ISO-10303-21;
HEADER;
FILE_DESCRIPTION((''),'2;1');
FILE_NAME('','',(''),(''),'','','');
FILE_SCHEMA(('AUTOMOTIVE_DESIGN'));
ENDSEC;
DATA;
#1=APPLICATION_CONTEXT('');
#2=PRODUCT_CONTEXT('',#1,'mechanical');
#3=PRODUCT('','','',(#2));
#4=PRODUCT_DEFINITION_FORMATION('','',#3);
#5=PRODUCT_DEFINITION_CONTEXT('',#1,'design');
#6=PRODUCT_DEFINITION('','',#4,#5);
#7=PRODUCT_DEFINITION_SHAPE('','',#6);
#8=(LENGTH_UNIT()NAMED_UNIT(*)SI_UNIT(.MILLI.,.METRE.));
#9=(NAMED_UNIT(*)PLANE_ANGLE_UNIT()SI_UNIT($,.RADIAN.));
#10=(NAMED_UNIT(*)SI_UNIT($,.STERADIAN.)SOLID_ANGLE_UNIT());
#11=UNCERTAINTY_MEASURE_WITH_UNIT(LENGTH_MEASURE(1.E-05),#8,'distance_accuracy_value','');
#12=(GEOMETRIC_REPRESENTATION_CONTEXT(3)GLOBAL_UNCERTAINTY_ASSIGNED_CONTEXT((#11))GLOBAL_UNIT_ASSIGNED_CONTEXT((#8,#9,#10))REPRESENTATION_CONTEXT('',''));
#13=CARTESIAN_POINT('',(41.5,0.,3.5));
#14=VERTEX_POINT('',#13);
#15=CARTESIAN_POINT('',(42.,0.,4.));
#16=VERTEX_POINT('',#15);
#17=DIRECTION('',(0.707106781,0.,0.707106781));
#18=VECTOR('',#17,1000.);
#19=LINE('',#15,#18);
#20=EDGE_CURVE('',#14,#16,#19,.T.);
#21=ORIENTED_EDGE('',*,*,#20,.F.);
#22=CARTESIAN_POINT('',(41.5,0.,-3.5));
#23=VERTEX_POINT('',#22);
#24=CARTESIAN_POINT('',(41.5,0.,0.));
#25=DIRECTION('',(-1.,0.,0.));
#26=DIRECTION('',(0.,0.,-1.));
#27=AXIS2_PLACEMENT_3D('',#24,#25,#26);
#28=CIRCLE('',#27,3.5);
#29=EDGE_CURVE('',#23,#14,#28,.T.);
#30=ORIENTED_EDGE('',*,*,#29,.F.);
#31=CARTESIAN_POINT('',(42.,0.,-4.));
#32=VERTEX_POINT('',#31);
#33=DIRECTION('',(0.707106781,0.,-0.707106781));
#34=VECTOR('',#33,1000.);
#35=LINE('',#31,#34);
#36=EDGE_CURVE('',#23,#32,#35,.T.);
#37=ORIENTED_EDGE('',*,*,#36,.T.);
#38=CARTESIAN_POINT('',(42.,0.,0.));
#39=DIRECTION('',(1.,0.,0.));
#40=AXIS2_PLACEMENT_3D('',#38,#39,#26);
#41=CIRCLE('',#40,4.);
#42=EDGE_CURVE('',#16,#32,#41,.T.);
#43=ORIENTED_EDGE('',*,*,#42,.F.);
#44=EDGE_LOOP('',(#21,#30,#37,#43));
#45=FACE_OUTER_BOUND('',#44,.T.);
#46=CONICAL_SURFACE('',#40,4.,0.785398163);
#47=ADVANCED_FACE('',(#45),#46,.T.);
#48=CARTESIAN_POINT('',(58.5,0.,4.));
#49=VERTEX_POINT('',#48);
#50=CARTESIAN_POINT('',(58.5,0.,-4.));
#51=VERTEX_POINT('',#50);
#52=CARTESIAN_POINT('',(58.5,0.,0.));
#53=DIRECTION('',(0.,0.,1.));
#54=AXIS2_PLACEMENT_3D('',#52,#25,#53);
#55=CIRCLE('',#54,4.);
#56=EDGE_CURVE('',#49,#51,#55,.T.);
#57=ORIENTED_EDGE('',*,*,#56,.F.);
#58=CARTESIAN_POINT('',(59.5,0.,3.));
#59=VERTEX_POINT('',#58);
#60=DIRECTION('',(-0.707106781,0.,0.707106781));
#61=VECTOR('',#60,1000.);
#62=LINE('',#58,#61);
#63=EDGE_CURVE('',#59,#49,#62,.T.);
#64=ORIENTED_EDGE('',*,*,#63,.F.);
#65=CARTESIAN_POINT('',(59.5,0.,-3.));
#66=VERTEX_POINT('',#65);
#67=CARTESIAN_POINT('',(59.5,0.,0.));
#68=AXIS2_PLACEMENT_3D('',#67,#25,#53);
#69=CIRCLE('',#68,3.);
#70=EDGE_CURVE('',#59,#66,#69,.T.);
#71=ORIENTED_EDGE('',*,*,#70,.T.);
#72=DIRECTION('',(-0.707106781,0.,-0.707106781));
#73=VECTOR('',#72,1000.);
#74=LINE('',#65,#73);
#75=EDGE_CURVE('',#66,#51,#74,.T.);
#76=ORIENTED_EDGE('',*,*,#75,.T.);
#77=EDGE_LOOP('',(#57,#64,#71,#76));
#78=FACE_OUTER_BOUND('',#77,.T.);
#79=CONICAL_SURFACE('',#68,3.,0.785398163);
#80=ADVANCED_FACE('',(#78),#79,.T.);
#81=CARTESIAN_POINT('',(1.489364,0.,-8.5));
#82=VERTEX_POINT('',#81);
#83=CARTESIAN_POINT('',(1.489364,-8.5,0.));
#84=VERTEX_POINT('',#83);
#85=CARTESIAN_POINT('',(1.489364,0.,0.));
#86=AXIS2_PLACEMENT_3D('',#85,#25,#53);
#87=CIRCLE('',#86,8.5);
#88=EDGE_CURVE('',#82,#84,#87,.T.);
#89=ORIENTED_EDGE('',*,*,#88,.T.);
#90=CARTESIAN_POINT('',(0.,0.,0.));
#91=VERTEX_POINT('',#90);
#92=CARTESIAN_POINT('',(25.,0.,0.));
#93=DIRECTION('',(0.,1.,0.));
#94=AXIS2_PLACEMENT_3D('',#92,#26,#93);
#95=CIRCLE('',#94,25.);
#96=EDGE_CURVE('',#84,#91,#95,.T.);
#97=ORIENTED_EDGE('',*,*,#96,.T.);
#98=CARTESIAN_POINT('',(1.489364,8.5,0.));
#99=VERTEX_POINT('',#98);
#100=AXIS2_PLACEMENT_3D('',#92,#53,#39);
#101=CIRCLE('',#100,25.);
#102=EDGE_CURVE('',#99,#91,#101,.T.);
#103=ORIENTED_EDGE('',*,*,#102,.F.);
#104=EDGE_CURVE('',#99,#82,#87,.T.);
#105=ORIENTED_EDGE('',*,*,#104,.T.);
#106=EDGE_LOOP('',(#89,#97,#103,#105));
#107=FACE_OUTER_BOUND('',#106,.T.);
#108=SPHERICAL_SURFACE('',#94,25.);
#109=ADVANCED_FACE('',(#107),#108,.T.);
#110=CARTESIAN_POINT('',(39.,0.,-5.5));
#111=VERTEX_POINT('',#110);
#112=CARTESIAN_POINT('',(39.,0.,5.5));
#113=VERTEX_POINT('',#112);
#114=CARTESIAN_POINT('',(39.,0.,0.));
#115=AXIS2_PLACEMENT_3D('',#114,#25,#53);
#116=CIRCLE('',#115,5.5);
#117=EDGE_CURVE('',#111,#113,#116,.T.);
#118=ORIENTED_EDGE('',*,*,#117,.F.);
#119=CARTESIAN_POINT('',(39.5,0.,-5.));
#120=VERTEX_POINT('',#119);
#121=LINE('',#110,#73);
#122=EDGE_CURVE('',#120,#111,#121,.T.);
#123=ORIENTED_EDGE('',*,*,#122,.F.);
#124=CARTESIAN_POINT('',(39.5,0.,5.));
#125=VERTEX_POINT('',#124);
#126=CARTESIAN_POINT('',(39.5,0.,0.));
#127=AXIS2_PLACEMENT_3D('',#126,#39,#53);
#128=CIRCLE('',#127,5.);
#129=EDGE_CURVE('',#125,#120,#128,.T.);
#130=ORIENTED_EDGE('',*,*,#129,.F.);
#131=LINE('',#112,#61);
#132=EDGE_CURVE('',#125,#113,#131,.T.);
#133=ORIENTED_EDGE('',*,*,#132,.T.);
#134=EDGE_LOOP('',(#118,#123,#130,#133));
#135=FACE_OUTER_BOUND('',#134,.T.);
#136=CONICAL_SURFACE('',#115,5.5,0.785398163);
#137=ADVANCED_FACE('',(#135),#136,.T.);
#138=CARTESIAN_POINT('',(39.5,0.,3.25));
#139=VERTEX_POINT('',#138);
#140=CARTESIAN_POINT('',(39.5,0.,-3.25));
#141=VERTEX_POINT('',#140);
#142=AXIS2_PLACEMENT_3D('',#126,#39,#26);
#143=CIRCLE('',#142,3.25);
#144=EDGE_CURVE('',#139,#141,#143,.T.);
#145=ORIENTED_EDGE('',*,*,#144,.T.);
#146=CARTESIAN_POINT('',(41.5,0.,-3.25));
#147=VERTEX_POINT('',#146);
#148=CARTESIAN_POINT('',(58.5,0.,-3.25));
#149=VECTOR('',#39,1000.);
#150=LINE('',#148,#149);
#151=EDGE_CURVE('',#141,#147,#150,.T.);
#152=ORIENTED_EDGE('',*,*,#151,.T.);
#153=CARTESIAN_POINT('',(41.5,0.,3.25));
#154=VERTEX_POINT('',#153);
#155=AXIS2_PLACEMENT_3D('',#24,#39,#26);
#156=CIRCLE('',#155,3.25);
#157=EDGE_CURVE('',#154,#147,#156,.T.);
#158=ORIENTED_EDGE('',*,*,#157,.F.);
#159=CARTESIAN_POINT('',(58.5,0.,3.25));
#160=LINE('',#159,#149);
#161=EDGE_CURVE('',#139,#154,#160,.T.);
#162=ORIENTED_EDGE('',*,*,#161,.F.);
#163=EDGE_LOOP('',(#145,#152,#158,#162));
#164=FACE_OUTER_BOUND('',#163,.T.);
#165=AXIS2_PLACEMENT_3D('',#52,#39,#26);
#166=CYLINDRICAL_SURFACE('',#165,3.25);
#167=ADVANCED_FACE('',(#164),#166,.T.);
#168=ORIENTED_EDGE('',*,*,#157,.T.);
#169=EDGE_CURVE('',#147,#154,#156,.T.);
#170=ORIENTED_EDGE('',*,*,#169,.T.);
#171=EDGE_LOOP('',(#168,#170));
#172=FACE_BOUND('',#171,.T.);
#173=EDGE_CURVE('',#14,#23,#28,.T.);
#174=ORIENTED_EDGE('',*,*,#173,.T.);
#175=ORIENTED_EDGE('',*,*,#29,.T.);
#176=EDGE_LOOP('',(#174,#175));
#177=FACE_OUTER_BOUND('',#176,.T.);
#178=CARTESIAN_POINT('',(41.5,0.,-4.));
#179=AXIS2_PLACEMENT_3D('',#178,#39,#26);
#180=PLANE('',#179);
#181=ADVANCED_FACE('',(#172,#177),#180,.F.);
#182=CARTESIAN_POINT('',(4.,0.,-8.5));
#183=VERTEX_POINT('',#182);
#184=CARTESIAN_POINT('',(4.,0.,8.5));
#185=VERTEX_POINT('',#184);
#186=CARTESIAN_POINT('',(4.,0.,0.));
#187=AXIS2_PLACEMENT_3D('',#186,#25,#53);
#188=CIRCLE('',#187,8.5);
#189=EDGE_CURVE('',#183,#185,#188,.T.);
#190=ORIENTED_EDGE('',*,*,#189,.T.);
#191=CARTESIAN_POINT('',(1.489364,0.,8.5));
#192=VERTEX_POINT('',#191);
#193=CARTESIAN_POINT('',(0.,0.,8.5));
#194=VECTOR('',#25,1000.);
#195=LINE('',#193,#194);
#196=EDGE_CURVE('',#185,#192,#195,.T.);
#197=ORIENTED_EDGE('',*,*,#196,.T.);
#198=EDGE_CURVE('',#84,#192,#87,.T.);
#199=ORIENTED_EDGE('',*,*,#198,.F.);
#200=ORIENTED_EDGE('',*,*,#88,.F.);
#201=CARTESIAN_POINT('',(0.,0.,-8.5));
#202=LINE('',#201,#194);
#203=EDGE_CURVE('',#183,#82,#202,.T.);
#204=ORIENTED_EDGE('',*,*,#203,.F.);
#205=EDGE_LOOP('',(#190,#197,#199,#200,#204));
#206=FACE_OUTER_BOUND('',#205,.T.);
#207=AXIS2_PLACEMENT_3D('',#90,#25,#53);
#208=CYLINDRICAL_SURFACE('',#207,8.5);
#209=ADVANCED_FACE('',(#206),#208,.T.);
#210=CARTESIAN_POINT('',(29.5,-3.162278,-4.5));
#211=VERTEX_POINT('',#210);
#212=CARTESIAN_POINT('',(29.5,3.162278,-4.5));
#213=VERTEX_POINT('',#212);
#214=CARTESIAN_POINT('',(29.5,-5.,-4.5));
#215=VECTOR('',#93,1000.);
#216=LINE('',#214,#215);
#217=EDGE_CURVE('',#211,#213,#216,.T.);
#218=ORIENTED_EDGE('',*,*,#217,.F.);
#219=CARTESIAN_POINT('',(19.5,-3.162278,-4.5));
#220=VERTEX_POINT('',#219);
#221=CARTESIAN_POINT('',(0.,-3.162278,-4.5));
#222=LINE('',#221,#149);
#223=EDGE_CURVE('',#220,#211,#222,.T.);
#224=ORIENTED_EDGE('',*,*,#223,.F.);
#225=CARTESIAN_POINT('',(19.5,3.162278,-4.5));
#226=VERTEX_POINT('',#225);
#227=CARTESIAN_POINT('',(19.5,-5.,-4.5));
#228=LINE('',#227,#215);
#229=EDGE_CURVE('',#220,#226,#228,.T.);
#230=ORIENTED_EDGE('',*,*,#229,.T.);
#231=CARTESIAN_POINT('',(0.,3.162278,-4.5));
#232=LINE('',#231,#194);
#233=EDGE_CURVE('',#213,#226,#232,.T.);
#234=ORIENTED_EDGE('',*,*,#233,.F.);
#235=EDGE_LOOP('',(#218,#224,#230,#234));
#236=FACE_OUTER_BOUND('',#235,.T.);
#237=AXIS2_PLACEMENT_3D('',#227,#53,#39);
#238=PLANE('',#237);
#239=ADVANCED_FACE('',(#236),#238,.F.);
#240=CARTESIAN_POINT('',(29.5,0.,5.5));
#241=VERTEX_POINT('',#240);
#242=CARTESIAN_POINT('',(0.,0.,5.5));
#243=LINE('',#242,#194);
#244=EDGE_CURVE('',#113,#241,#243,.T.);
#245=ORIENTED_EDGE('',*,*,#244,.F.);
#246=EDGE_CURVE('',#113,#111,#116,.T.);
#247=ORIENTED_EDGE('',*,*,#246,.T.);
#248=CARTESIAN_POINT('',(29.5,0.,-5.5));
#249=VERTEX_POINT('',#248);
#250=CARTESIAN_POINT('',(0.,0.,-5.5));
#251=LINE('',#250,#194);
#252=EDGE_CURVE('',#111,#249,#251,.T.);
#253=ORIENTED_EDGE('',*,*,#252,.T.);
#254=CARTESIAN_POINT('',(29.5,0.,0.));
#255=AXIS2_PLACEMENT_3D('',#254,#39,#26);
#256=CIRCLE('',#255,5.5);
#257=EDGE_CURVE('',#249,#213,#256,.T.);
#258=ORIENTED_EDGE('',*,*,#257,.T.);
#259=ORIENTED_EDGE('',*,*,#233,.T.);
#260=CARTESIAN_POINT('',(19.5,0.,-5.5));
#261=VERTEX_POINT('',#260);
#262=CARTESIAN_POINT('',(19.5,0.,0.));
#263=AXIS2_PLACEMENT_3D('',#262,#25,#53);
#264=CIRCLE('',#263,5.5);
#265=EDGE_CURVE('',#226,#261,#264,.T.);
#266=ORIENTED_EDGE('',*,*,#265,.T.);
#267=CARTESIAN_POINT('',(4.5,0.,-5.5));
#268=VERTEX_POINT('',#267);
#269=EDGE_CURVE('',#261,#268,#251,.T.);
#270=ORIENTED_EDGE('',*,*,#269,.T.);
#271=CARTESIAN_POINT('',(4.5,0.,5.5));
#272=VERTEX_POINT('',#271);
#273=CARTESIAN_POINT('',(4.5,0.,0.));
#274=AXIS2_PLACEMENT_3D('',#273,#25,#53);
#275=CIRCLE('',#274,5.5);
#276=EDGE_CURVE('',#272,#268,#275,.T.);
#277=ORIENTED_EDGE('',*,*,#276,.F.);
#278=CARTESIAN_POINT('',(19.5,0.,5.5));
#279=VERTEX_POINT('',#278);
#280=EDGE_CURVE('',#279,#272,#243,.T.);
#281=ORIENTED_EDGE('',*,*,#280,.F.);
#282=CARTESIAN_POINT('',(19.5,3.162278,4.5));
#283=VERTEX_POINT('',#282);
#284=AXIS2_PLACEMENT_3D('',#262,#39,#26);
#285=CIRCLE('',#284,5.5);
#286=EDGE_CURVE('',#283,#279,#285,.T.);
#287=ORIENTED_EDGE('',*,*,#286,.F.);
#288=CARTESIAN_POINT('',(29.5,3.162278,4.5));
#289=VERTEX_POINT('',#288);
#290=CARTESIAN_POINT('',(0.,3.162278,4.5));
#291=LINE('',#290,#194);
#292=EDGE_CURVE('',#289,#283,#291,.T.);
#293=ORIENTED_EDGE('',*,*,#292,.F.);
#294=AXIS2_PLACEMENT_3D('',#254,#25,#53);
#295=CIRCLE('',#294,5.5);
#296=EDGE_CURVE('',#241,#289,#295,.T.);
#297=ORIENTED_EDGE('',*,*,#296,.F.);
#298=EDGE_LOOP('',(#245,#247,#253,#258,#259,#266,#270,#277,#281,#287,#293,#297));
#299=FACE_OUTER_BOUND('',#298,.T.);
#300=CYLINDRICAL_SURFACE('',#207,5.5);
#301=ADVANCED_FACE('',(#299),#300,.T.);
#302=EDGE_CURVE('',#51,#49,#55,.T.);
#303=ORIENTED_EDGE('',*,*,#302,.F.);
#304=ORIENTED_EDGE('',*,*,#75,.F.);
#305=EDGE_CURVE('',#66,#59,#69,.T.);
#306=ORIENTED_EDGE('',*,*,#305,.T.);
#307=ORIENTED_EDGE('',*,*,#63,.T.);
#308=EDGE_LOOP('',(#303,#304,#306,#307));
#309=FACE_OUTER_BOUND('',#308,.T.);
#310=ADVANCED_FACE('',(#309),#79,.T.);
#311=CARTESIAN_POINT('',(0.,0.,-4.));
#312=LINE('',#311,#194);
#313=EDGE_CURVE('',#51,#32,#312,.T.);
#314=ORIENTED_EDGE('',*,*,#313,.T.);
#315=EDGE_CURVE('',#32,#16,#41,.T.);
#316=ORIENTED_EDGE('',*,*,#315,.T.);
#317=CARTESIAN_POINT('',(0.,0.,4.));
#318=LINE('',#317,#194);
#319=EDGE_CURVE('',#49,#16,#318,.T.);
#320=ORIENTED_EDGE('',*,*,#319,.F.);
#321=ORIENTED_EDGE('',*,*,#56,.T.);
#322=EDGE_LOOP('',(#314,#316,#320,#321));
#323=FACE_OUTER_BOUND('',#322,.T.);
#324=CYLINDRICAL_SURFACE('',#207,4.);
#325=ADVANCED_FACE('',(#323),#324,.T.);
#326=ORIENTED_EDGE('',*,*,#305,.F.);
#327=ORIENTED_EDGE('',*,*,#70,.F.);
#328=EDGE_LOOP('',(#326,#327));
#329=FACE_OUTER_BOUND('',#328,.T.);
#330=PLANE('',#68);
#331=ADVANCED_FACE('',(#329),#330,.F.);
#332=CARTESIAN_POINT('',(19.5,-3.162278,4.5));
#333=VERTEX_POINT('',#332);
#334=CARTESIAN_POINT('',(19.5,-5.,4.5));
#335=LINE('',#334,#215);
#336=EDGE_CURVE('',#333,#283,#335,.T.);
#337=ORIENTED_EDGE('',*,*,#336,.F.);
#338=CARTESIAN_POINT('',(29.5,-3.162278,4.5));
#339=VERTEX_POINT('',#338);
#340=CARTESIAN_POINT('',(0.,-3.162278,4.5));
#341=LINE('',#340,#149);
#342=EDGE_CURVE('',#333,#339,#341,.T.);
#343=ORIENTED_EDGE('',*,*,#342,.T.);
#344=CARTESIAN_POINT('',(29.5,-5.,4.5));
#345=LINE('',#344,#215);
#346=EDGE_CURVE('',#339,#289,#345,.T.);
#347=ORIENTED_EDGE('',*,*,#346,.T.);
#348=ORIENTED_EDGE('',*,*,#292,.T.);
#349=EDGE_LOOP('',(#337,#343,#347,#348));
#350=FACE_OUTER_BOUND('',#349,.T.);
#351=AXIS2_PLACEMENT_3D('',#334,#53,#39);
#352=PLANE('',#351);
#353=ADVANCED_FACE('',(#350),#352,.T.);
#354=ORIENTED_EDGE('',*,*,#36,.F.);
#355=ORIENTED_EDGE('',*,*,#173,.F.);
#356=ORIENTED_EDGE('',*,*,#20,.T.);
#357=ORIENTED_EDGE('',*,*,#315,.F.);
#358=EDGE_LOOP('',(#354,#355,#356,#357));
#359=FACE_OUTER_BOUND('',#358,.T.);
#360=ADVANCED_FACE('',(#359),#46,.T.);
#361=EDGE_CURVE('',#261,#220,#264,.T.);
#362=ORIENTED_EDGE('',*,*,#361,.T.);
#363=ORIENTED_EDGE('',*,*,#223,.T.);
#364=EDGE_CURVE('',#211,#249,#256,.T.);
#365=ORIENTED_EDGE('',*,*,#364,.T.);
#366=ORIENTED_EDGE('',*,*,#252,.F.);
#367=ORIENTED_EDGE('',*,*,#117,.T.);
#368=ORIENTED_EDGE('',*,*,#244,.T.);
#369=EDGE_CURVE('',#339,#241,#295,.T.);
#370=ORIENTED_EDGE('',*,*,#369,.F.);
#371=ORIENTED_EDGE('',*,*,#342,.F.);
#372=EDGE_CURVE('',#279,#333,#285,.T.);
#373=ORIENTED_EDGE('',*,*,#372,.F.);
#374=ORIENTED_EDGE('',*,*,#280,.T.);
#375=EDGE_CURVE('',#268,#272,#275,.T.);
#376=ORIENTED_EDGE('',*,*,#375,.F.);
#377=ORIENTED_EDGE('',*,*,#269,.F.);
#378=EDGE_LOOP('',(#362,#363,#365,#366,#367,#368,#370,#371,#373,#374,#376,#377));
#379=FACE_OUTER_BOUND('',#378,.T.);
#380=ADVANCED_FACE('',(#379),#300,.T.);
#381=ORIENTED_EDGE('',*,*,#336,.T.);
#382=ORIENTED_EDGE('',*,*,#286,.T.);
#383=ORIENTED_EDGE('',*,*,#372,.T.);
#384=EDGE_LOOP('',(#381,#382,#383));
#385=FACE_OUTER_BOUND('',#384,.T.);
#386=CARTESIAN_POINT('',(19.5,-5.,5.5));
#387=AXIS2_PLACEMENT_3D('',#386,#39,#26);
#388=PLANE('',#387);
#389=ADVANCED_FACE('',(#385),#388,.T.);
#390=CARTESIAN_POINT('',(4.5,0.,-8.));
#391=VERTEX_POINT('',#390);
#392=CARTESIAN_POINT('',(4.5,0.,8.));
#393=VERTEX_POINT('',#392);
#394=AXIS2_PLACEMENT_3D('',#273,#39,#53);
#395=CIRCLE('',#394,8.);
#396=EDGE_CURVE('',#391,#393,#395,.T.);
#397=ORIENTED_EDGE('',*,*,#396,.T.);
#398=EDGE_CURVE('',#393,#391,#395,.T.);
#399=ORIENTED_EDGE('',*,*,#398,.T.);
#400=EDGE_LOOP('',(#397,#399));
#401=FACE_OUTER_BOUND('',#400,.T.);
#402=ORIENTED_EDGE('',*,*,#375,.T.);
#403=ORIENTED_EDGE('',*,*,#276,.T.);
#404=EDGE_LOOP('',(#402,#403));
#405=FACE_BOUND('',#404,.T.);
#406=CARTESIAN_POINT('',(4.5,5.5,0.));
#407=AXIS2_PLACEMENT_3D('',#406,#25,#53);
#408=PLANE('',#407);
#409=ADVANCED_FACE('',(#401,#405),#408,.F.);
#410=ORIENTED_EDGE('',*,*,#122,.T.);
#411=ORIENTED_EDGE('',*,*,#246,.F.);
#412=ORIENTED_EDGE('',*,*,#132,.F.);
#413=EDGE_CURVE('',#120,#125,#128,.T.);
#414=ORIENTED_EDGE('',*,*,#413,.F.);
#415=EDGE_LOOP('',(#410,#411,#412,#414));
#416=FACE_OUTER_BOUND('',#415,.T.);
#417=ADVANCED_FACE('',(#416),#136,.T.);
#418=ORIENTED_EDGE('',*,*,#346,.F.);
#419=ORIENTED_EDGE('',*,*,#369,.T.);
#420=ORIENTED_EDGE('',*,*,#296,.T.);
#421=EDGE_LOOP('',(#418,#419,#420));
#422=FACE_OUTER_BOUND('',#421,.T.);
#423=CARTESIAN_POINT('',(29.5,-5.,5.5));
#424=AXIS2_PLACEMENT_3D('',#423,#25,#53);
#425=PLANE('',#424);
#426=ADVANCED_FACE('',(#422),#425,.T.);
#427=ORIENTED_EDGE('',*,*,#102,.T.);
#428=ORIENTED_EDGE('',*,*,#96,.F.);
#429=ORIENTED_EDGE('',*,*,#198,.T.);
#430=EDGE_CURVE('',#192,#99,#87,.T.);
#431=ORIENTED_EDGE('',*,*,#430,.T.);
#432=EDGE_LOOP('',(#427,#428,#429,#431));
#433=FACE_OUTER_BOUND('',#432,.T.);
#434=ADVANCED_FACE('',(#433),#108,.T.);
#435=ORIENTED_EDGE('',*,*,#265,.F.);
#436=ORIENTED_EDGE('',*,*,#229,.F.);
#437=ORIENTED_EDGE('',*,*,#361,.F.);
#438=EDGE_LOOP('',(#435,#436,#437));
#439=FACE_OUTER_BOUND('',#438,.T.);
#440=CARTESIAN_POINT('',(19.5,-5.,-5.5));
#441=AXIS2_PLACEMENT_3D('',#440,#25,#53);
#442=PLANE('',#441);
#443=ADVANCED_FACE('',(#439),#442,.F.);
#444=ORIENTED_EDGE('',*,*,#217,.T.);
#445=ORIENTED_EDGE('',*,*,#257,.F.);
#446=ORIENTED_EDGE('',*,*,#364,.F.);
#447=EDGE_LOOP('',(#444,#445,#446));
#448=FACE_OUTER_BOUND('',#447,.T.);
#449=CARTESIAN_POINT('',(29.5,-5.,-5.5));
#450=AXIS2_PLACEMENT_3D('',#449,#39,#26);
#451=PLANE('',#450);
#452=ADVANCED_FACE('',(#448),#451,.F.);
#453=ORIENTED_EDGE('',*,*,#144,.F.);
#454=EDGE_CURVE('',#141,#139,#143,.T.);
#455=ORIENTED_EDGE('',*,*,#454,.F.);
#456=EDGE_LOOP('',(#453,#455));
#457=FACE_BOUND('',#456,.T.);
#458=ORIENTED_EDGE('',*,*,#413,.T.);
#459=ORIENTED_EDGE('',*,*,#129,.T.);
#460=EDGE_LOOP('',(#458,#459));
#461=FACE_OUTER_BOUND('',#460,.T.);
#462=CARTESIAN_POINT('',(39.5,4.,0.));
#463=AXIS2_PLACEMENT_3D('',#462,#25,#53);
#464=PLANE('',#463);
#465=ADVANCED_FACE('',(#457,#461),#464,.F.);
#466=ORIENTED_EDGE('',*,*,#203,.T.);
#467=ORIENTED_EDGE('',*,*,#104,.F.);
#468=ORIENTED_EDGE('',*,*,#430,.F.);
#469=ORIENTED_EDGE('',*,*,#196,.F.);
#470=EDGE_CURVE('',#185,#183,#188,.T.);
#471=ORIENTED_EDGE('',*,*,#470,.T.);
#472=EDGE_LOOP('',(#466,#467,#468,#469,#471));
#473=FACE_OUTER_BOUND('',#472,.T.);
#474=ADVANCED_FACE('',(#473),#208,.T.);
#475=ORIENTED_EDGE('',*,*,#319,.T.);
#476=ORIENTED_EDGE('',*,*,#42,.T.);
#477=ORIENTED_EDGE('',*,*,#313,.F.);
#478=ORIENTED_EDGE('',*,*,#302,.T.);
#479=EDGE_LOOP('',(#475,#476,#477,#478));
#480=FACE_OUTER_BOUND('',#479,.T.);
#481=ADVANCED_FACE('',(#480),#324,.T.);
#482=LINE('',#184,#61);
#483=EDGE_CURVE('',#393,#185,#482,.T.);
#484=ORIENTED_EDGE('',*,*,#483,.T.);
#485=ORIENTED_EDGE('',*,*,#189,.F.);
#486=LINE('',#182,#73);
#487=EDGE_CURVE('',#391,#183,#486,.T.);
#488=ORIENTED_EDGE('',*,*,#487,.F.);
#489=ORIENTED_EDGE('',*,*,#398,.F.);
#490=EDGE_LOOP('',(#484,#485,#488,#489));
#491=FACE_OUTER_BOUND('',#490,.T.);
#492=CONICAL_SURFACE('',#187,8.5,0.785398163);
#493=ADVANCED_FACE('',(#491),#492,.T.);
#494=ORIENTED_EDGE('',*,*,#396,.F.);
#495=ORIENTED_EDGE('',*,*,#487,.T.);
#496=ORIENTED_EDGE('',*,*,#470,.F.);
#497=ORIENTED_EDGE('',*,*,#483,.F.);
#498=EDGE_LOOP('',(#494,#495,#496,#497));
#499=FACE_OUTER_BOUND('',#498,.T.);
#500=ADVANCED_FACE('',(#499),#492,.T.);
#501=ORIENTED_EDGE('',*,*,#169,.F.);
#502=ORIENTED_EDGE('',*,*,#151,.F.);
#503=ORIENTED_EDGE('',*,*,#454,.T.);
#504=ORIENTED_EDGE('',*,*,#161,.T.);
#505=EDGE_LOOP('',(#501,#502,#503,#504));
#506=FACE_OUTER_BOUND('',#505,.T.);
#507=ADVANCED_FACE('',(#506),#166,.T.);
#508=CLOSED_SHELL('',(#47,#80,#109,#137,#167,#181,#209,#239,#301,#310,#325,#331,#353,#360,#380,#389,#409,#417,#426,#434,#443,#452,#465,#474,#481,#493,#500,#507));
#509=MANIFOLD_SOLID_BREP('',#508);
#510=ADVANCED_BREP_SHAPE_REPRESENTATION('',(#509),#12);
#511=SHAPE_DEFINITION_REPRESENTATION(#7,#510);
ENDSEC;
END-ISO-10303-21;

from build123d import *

# Parameters (mm, degrees)
SKETCH2_W          = 10
SKETCH2_H          = 1
CUT_EXTRUDE2_DEPTH = 5
CHAMFER1_SIZE      = 0.5
SKETCH3_W          = 2
SKETCH3_H          = 0.75
CHAMFER2_SIZE      = 0.5


with BuildPart() as part:
    # Sketch1 → Revolve1 (revolve)
    with BuildSketch(Plane.XY, mode=Mode.PRIVATE) as revolve1_sk:
        with BuildLine():
            Line((59.5, 3), (58.5, 4))
            Line((58.5, 4), (39.5, 4))
            Line((39.5, 4), (39.5, 5.5))
            Line((39.5, 5.5), (4.5, 5.5))
            Line((4.5, 5.5), (4.5, 8.5))
            Line((4.5, 8.5), (1.489364109, 8.5))
            ThreePointArc((1.489364109, 8.5), (0.375155866, 4.314748123), (0, 0))
            Line((0, 0), (59.5, 0))
            Line((59.5, 0), (59.5, 3))
        make_face()
    revolve(revolve1_sk.sketch.rotate(Axis((0, 0, 0), (1, 0, 0)), 90), axis=Axis((0, 0, 0), (1, 0, 0)))

    # Sketch2 → Cut-Extrude2 (cut, symmetric)
    with BuildSketch(Plane(origin=(0, 0, 0), x_dir=(1, 0, 0), z_dir=(0, 1, 0))):
        with Locations((24.5, 5)):
            Rectangle(SKETCH2_W, SKETCH2_H)
    cut_extrude2 = extrude(amount=CUT_EXTRUDE2_DEPTH, both=True, mode=Mode.SUBTRACT)

    # Mirror1: Cut-Extrude2 across plane
    add(cut_extrude2.mirror(Plane.XY), mode=Mode.SUBTRACT)

    # Chamfer1
    chamfer1_edges = [part.edges().sort_by_distance(p)[0] for p in [
        (4.5, 0, -8.5),
        (39.5, 0, -5.5),
    ]]
    chamfer(chamfer1_edges, length=CHAMFER1_SIZE)

    # Sketch3 → Cut-Revolve1 (revolve, cut)
    with BuildSketch(Plane(origin=(0, 0, 0), x_dir=(1, 0, 0), z_dir=(0, 1, 0)), mode=Mode.PRIVATE) as cut_revolve1_sk:
        with Locations((40.5, 3.625)):
            Rectangle(SKETCH3_W, SKETCH3_H)
    revolve(cut_revolve1_sk.sketch.rotate(Axis((58.5, 0, 0), (-1, 0, 0)), 270), axis=Axis((58.5, 0, 0), (-1, 0, 0)), mode=Mode.SUBTRACT)

    # Chamfer2
    chamfer2_edges = [part.edges().sort_by_distance(p)[0] for p in [
        (41.5, 0, -4),
    ]]
    chamfer(chamfer2_edges, length=CHAMFER2_SIZE)


solid = part.part
